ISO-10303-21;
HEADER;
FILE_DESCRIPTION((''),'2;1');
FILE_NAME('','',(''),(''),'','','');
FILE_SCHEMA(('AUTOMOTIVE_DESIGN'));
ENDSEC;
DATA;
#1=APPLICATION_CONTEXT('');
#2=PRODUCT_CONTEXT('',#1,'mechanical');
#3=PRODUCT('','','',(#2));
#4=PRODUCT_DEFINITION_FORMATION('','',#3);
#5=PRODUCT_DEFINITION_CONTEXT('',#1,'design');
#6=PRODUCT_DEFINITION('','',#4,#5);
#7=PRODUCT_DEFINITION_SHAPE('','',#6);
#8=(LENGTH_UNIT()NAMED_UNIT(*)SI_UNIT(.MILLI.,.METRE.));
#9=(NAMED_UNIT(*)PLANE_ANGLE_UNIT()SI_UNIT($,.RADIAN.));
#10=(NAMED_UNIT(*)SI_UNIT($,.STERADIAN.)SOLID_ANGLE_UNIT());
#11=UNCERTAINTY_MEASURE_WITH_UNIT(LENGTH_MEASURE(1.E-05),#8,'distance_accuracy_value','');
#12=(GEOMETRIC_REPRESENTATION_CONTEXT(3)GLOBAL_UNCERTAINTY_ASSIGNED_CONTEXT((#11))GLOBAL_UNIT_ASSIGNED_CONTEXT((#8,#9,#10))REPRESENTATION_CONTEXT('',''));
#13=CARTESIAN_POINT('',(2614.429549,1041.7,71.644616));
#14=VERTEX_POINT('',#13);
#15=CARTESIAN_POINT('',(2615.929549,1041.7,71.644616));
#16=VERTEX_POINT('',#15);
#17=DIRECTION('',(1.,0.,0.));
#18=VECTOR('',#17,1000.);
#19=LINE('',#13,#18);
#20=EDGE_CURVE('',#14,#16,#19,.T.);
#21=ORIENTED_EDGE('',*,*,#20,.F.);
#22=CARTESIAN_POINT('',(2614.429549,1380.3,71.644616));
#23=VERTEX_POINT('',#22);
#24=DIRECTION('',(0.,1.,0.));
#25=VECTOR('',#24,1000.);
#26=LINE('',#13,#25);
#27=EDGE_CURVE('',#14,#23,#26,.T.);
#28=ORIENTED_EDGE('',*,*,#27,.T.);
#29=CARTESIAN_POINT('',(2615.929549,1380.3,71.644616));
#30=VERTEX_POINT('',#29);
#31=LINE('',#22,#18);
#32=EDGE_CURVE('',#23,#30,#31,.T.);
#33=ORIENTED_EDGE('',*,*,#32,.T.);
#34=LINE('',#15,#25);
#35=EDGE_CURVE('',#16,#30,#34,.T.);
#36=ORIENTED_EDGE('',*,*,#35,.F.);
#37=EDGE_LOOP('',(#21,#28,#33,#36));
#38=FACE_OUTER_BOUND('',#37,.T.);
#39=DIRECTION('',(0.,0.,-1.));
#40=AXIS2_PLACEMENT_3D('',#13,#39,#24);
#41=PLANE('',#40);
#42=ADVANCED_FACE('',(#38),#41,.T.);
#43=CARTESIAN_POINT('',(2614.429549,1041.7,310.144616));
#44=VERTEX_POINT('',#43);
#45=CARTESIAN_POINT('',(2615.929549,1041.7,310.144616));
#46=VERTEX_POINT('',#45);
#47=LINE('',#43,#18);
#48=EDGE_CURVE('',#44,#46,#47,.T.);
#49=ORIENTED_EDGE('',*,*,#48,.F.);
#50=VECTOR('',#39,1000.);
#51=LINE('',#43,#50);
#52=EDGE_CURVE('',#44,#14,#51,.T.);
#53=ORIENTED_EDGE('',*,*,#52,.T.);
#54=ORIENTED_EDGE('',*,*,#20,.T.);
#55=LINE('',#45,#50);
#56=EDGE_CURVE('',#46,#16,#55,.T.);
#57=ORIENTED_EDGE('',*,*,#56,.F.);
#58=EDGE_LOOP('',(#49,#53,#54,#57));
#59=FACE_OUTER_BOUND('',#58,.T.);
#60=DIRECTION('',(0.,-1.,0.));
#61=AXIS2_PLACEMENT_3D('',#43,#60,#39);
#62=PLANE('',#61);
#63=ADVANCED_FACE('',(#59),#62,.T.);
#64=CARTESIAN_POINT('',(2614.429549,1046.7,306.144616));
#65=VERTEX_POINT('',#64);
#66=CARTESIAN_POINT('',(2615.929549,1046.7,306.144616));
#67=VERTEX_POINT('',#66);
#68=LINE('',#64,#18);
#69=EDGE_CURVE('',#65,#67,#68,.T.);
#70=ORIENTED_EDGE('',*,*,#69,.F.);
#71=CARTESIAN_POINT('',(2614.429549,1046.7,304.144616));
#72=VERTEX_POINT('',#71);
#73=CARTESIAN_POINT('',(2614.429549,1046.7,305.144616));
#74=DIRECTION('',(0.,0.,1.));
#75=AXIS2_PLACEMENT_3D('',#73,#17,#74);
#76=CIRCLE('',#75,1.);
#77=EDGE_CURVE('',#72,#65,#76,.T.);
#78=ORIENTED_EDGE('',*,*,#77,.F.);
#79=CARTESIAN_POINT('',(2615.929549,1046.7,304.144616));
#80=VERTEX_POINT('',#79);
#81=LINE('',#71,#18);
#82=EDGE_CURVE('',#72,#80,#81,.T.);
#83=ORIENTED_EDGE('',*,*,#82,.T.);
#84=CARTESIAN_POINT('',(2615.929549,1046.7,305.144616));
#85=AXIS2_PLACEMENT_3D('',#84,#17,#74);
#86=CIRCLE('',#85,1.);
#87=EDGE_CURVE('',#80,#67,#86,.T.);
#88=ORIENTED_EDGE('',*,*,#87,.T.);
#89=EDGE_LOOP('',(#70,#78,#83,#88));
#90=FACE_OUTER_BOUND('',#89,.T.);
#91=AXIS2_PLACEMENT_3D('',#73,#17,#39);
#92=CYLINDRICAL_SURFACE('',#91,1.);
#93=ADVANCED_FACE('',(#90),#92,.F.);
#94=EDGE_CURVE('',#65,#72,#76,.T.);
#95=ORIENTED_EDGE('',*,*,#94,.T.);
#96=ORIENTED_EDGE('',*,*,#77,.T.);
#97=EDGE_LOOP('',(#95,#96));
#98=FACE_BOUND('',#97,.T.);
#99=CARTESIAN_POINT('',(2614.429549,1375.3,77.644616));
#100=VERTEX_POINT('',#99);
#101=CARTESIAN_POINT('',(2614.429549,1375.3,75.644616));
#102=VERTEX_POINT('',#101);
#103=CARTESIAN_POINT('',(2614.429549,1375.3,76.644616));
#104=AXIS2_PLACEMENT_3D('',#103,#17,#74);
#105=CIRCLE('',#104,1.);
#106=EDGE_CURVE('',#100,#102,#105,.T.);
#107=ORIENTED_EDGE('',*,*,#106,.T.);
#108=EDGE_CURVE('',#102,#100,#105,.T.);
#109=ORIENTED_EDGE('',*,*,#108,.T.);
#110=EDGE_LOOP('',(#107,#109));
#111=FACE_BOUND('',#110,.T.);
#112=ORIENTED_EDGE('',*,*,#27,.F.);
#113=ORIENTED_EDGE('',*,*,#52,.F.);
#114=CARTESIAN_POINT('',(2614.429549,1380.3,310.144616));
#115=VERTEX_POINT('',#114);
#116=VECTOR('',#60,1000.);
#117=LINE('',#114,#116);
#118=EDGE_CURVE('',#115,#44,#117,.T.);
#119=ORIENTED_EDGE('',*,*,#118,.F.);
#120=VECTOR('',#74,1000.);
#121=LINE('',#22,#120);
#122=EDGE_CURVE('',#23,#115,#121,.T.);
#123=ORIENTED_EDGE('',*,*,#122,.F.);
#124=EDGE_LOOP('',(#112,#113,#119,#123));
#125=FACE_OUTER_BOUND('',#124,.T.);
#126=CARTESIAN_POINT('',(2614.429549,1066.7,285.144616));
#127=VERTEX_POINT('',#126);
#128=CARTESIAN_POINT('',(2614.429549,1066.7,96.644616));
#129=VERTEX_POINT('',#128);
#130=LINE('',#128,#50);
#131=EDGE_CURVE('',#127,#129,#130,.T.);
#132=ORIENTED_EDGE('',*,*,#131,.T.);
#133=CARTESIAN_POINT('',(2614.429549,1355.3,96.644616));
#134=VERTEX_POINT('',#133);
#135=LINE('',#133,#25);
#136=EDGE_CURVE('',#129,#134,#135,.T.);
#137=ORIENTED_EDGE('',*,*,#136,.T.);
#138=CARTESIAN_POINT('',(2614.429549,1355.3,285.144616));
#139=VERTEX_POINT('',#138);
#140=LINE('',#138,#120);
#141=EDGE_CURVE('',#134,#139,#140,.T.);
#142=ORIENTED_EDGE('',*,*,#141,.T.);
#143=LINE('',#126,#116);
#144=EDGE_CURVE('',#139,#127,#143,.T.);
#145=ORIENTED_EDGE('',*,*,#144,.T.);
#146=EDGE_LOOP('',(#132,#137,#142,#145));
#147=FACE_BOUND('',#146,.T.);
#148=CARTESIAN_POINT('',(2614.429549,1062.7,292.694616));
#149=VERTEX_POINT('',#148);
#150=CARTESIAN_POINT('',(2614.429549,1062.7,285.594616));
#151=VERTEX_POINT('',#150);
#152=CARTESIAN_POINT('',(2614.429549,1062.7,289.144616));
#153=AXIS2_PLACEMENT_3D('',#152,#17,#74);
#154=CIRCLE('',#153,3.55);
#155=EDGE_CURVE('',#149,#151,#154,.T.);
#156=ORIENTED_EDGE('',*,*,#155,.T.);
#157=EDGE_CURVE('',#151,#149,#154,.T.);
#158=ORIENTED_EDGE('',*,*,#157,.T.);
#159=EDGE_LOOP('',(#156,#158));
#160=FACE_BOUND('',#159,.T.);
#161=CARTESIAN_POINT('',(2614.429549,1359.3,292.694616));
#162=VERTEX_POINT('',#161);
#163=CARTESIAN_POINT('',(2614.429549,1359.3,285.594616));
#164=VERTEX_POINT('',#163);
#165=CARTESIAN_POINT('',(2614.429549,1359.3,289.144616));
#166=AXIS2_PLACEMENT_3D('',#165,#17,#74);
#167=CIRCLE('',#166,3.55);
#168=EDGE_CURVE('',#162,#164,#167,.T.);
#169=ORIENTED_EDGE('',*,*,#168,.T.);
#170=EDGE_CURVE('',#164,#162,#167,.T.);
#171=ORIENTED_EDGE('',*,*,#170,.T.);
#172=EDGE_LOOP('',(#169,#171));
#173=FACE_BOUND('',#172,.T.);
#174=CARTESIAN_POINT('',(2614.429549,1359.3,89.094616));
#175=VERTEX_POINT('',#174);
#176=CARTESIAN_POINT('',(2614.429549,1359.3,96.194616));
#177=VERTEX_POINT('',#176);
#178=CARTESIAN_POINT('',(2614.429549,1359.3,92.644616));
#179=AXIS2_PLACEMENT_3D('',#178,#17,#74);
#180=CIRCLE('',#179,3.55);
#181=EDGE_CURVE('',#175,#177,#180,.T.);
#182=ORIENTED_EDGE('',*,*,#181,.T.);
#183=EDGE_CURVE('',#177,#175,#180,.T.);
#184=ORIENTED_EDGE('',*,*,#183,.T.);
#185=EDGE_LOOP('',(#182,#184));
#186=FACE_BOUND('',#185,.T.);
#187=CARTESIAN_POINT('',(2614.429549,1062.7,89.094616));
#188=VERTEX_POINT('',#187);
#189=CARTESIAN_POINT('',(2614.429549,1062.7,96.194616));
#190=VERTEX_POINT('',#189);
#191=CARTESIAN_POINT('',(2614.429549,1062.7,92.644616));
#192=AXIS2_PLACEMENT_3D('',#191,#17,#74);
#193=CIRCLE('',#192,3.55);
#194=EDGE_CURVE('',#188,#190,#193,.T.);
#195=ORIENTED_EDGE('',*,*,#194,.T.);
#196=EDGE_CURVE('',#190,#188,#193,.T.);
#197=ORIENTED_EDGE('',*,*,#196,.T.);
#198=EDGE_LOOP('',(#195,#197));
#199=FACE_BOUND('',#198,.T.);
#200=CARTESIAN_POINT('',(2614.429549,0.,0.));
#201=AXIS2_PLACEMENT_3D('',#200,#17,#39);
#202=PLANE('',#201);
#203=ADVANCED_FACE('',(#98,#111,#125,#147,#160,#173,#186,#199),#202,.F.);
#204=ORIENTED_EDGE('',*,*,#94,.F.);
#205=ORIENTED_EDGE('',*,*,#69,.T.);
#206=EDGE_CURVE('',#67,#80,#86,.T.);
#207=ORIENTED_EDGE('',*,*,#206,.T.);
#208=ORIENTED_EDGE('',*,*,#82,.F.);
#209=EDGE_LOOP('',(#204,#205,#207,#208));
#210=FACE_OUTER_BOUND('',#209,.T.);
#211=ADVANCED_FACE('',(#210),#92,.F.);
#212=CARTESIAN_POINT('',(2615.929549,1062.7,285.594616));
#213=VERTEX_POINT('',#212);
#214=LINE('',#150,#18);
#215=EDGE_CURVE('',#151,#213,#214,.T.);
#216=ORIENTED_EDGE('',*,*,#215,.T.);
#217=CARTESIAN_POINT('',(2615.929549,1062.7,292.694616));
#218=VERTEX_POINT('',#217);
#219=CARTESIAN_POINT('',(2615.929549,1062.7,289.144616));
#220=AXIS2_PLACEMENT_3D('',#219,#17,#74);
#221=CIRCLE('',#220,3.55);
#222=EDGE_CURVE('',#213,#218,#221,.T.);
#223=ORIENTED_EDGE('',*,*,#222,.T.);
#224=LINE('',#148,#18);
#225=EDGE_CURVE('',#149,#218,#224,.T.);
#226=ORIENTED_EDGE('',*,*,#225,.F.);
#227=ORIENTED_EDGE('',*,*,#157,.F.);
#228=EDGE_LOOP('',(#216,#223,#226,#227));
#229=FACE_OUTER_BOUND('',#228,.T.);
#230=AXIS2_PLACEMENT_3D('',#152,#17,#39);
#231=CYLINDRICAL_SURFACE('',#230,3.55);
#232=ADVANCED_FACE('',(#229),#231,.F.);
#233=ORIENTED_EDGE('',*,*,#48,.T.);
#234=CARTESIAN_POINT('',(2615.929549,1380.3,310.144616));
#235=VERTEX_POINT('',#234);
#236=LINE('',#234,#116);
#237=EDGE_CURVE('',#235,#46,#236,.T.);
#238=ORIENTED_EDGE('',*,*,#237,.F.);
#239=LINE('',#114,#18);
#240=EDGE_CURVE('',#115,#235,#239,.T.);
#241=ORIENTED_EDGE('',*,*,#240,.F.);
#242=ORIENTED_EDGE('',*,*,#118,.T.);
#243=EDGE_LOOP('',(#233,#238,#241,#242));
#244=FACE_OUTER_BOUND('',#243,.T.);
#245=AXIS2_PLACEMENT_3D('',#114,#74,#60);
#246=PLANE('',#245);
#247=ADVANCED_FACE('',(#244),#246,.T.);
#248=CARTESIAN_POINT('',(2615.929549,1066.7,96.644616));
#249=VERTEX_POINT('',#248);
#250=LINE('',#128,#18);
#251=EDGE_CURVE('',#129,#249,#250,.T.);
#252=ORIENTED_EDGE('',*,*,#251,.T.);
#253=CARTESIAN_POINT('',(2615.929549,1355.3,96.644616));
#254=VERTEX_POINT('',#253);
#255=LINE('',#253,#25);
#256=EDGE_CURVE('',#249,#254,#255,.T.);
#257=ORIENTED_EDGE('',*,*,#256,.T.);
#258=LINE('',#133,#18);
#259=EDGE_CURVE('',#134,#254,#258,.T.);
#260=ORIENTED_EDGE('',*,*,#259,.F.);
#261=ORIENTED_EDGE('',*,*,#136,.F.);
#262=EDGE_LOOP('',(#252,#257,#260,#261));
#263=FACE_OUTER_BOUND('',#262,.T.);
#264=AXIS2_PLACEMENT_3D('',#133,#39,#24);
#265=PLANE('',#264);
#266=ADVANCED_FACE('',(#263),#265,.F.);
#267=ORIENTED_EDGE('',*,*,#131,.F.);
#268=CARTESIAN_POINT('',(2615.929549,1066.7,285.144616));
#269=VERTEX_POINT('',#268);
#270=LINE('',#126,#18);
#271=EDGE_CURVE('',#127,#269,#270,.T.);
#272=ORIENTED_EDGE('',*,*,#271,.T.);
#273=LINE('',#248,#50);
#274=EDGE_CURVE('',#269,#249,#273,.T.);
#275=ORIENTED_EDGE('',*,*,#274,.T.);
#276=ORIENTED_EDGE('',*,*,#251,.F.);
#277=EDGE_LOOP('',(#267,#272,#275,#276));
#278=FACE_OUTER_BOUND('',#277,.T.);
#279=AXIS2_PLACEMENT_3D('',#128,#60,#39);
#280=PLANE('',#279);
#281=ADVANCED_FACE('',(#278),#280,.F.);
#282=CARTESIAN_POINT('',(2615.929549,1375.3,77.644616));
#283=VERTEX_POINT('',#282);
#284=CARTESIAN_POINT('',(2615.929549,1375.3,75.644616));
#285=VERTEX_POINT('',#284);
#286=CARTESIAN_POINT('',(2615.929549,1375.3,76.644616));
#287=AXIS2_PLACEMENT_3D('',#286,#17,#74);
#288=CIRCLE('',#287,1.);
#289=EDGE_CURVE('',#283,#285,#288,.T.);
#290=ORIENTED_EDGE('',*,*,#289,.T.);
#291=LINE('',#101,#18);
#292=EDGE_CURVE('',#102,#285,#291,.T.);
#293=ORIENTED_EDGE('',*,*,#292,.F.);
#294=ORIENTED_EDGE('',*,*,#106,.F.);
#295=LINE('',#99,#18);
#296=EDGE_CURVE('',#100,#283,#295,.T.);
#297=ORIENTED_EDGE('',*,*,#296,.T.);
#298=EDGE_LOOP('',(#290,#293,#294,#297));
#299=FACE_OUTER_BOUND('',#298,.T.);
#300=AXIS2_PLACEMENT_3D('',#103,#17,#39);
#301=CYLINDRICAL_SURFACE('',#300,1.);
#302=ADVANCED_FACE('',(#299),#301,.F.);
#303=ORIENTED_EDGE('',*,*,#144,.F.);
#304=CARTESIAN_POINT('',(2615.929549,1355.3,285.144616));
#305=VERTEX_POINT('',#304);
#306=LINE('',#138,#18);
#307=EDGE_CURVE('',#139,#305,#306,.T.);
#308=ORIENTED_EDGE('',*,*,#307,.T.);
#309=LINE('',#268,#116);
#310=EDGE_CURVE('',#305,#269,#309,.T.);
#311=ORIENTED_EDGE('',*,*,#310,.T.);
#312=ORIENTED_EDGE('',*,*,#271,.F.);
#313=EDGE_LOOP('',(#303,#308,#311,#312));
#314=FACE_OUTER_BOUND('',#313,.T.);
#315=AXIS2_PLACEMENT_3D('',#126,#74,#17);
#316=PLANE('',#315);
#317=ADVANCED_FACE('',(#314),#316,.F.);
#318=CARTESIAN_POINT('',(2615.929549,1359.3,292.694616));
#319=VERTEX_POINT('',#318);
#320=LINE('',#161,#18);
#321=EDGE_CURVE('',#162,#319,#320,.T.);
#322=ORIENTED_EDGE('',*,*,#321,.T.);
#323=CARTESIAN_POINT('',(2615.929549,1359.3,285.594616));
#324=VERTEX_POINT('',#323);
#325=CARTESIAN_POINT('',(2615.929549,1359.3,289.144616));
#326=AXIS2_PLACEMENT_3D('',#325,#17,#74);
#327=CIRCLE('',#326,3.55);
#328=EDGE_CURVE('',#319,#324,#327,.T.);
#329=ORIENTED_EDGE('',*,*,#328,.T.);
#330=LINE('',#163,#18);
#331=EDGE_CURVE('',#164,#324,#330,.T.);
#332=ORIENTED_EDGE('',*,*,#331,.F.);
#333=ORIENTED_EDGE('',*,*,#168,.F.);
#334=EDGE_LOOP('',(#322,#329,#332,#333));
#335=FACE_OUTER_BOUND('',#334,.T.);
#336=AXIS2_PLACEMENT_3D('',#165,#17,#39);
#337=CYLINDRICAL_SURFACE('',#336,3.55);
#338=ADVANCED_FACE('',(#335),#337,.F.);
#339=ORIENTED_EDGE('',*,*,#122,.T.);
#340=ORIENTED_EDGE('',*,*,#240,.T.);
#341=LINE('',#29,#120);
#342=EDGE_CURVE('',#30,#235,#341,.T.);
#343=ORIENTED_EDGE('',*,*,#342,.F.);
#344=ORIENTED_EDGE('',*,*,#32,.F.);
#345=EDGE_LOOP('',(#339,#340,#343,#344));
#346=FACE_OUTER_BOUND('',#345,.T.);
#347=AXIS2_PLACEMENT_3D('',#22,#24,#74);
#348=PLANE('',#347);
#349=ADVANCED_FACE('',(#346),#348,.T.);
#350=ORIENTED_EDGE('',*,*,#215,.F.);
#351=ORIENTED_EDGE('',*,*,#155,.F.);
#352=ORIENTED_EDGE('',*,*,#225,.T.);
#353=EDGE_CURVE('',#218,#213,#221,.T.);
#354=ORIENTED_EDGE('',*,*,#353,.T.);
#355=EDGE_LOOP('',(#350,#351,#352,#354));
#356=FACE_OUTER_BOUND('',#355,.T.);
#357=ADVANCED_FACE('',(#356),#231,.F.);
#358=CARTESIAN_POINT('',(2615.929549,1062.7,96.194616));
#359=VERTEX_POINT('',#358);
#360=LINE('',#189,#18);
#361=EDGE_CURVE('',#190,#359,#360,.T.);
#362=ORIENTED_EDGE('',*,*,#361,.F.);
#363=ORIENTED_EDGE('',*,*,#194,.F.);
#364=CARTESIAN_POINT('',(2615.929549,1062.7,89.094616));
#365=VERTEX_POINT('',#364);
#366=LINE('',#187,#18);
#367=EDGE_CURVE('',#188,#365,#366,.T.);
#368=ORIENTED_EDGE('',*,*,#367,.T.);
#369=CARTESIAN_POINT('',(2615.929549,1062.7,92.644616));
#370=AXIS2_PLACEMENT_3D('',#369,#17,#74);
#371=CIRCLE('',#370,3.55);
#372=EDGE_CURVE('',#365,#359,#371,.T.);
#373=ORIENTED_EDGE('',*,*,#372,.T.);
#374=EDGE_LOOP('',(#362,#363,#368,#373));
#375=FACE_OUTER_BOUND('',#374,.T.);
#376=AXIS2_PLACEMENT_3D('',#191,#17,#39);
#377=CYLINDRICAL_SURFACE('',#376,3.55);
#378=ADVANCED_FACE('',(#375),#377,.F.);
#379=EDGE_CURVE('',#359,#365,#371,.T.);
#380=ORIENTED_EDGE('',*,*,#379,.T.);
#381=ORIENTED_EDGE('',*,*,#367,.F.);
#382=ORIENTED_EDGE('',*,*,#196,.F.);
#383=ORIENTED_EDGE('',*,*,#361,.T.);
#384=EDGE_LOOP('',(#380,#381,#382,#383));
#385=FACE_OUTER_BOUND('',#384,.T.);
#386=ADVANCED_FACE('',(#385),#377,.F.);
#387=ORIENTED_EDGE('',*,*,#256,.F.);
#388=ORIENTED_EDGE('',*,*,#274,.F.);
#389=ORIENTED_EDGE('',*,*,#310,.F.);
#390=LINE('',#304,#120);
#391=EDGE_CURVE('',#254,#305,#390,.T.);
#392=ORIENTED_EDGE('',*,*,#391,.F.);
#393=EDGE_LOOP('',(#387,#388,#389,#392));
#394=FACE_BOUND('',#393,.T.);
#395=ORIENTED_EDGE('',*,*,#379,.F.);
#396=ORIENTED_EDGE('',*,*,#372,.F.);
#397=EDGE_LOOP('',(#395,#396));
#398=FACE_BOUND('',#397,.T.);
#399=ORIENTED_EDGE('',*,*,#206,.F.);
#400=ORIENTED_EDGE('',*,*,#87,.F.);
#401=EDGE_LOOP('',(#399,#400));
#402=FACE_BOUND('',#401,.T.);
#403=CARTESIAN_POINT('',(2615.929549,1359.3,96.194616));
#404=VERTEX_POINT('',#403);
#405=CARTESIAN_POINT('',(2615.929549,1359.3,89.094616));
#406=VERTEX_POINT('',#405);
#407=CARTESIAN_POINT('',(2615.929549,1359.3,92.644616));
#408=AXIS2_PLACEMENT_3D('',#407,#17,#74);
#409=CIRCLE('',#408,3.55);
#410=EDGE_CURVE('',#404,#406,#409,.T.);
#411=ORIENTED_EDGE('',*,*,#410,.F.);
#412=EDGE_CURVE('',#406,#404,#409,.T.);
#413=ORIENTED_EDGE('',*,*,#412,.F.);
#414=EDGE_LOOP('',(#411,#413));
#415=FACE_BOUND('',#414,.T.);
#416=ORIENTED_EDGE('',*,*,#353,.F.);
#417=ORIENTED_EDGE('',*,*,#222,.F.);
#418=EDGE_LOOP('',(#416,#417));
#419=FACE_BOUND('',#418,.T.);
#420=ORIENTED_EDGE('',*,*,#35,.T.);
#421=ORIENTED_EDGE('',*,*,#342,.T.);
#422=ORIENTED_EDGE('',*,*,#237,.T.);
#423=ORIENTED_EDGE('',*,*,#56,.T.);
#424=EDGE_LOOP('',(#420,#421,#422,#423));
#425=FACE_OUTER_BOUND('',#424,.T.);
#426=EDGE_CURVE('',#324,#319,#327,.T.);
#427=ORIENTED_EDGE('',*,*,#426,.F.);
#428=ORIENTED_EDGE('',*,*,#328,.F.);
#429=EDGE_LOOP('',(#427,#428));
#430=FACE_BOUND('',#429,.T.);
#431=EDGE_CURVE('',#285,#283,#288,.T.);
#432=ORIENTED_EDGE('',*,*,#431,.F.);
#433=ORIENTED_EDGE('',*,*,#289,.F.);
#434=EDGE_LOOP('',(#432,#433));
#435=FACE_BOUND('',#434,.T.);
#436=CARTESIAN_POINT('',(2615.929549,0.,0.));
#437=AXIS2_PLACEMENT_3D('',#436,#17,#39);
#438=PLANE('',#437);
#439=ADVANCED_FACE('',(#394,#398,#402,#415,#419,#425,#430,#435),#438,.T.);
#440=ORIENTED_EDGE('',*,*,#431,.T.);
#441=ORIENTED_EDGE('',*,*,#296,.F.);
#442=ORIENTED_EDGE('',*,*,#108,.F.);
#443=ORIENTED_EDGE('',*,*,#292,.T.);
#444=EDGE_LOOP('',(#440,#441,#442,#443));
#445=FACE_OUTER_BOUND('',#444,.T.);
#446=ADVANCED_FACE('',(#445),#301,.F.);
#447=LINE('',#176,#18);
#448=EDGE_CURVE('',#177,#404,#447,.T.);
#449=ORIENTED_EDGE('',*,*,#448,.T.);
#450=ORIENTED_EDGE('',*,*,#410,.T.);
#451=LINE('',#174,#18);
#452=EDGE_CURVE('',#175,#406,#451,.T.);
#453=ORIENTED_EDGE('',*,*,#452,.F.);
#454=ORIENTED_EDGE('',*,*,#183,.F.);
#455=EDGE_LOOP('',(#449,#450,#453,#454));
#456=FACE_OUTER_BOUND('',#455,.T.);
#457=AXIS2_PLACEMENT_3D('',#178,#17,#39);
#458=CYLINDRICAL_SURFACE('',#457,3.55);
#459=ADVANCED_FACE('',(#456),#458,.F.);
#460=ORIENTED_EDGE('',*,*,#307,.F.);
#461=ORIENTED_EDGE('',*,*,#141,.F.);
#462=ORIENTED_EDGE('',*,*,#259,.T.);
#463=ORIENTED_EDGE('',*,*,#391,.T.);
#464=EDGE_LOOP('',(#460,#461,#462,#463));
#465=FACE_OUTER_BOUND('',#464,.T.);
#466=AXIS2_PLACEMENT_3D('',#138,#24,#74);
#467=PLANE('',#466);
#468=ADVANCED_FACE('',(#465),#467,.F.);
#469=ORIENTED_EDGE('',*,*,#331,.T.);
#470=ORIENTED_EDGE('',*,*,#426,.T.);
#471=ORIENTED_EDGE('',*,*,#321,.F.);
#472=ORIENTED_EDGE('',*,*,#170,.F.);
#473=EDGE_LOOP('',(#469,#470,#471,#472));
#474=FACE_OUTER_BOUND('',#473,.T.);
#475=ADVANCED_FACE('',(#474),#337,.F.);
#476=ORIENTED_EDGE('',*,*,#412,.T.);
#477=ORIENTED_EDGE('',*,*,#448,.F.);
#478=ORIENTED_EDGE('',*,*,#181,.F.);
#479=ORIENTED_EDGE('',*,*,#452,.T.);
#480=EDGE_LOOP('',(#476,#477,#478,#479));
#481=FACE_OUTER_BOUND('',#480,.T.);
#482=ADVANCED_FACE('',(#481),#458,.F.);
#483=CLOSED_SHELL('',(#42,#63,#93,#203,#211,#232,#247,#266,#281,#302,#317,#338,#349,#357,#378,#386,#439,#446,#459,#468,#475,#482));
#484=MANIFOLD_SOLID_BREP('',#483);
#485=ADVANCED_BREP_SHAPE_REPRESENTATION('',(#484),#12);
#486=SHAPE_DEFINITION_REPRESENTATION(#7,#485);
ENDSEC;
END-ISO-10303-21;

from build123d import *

# Parameters (mm, degrees)
SKETCH_1_W      = 238.5
SKETCH_1_H      = 338.6
SKETCH_1_R      = 1
SKETCH_1_R_2    = 3.55
SKETCH_1_W_2    = 188.5
SKETCH_1_H_2    = 288.6
EXTRUDE_1_DEPTH = 1.5


with BuildPart() as part:
    # 草图1 → 凸台-拉伸1 (new body)
    with BuildSketch(Plane(origin=(2615.929548806, 0, 0), x_dir=(0, 0, -1), z_dir=(1, 0, 0))):
        with Locations((-190.894615796, 1211)):
            Rectangle(SKETCH_1_W, SKETCH_1_H)
        with Locations(Location((-305.144615796, 1046.7, 0), (0, 0, 180))):
            Circle(SKETCH_1_R, mode=Mode.SUBTRACT)
        with Locations(Location((-76.644615796, 1375.3, 0), (0, 0, 180))):
            Circle(SKETCH_1_R, mode=Mode.SUBTRACT)
        with Locations(Location((-289.144615796, 1062.7, 0), (0, 0, 180))):
            Circle(SKETCH_1_R_2, mode=Mode.SUBTRACT)
        with Locations(Location((-92.644615796, 1359.3, 0), (0, 0, 180))):
            Circle(SKETCH_1_R_2, mode=Mode.SUBTRACT)
        with Locations(Location((-92.644615796, 1062.7, 0), (0, 0, 180))):
            Circle(SKETCH_1_R_2, mode=Mode.SUBTRACT)
        with Locations(Location((-289.144615796, 1359.3, 0), (0, 0, 180))):
            Circle(SKETCH_1_R_2, mode=Mode.SUBTRACT)
        with Locations((-190.894615796, 1211)):
            Rectangle(SKETCH_1_W_2, SKETCH_1_H_2, mode=Mode.SUBTRACT)
    extrude(amount=-EXTRUDE_1_DEPTH)


solid = part.part
